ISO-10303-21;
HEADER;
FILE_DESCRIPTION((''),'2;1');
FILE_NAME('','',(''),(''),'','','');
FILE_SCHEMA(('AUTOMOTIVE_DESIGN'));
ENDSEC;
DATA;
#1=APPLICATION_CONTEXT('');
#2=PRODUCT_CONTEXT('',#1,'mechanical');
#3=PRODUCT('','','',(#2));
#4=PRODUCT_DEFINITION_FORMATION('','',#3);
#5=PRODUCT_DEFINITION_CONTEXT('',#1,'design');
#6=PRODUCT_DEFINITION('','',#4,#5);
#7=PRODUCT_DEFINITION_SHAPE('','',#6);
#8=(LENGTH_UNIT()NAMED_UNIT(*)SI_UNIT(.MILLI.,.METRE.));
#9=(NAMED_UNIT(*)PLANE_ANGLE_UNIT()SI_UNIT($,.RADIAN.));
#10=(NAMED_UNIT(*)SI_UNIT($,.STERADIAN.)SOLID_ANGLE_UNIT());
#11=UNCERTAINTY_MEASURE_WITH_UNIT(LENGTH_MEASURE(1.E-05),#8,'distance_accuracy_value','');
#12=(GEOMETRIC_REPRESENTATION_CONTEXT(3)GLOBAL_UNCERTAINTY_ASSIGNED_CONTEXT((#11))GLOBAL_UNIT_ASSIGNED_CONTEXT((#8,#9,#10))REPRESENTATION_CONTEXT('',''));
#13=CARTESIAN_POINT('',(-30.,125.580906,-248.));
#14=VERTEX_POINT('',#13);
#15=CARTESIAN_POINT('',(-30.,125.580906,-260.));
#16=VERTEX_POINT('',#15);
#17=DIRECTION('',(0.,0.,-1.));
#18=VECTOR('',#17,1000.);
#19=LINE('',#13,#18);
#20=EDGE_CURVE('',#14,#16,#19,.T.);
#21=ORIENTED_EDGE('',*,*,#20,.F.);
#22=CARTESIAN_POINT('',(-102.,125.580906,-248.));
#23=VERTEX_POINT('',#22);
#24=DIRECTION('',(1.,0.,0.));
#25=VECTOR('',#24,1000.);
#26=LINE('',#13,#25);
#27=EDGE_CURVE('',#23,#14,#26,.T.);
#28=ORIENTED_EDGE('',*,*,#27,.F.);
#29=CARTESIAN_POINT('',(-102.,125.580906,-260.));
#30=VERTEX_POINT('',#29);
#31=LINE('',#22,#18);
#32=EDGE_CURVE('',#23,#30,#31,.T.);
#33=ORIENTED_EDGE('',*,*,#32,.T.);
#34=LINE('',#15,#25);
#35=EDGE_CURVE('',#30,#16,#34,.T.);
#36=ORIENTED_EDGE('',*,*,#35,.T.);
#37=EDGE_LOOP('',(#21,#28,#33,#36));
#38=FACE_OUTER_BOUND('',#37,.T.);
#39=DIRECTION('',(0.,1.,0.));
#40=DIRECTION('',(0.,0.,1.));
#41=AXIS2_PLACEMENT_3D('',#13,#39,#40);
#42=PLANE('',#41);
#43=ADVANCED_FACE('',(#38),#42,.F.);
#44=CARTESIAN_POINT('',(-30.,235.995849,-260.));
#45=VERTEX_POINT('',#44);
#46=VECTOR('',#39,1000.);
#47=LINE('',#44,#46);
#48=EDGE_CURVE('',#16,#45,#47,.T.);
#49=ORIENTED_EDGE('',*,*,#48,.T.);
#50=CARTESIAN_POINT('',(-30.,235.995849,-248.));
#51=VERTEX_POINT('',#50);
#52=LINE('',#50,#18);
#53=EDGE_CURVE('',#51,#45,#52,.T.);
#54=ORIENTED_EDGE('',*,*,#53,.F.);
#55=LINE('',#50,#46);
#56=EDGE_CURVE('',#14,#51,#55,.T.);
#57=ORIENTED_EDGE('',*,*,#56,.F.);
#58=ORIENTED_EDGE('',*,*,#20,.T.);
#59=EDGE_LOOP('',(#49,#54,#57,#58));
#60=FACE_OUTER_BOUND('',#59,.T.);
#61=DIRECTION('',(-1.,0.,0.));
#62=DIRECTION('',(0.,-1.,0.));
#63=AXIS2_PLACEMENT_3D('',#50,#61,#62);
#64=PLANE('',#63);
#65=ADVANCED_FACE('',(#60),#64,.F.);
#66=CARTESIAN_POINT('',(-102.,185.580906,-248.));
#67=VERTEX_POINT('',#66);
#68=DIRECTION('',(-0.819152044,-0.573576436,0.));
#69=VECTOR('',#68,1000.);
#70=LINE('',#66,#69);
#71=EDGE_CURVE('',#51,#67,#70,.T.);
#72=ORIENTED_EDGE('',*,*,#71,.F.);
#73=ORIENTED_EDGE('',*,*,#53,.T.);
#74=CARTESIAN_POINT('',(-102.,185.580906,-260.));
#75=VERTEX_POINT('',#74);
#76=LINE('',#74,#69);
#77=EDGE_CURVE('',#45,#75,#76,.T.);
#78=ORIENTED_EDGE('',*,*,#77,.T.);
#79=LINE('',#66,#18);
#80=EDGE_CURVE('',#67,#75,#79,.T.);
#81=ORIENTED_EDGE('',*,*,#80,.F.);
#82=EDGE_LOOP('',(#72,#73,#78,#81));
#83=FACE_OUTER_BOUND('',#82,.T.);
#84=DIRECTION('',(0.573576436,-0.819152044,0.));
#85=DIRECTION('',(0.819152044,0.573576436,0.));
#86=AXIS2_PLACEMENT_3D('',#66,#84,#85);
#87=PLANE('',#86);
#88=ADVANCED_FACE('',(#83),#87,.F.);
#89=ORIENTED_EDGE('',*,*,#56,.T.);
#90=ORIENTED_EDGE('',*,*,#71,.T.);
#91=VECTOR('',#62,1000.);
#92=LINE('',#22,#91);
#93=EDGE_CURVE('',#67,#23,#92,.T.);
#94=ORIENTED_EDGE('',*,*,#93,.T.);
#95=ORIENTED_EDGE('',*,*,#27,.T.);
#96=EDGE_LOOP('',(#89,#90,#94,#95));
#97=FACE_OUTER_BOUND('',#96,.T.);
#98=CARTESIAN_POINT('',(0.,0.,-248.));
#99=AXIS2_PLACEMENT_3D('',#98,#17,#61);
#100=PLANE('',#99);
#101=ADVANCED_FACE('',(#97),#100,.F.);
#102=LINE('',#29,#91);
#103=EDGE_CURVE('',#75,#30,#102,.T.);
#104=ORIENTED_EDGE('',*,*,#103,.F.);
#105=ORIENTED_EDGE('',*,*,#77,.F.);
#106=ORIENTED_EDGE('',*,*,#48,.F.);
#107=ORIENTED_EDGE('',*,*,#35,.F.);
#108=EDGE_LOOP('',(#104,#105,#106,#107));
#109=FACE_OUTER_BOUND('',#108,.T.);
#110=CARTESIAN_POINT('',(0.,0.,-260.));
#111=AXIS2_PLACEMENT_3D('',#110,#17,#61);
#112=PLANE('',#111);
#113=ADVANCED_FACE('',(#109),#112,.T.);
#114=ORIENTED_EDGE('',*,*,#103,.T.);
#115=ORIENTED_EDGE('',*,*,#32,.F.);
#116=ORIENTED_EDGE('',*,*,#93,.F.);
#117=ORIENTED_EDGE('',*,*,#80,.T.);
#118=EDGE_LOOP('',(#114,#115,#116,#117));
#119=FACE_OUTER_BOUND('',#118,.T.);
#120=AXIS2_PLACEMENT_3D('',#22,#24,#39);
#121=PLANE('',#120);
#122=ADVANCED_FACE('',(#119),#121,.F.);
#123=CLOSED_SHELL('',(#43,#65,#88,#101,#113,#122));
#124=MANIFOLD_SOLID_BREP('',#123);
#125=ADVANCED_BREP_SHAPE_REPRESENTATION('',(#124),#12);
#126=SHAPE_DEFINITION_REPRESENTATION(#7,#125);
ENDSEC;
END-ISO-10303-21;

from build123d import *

# Parameters (mm, degrees)
EXTRUDE_START   = -260
EXTRUDE_1_DEPTH = 12


with BuildPart() as part:
    # 草图1 → 凸台-拉伸1 (new body)
    with BuildSketch(Plane.XY.offset(EXTRUDE_START)):
        Polygon((-102, 125.580906485), (-102, 185.580906485), (-30, 235.995849236), (-30, 125.580906485), align=None)
    extrude(amount=EXTRUDE_1_DEPTH)


solid = part.part
